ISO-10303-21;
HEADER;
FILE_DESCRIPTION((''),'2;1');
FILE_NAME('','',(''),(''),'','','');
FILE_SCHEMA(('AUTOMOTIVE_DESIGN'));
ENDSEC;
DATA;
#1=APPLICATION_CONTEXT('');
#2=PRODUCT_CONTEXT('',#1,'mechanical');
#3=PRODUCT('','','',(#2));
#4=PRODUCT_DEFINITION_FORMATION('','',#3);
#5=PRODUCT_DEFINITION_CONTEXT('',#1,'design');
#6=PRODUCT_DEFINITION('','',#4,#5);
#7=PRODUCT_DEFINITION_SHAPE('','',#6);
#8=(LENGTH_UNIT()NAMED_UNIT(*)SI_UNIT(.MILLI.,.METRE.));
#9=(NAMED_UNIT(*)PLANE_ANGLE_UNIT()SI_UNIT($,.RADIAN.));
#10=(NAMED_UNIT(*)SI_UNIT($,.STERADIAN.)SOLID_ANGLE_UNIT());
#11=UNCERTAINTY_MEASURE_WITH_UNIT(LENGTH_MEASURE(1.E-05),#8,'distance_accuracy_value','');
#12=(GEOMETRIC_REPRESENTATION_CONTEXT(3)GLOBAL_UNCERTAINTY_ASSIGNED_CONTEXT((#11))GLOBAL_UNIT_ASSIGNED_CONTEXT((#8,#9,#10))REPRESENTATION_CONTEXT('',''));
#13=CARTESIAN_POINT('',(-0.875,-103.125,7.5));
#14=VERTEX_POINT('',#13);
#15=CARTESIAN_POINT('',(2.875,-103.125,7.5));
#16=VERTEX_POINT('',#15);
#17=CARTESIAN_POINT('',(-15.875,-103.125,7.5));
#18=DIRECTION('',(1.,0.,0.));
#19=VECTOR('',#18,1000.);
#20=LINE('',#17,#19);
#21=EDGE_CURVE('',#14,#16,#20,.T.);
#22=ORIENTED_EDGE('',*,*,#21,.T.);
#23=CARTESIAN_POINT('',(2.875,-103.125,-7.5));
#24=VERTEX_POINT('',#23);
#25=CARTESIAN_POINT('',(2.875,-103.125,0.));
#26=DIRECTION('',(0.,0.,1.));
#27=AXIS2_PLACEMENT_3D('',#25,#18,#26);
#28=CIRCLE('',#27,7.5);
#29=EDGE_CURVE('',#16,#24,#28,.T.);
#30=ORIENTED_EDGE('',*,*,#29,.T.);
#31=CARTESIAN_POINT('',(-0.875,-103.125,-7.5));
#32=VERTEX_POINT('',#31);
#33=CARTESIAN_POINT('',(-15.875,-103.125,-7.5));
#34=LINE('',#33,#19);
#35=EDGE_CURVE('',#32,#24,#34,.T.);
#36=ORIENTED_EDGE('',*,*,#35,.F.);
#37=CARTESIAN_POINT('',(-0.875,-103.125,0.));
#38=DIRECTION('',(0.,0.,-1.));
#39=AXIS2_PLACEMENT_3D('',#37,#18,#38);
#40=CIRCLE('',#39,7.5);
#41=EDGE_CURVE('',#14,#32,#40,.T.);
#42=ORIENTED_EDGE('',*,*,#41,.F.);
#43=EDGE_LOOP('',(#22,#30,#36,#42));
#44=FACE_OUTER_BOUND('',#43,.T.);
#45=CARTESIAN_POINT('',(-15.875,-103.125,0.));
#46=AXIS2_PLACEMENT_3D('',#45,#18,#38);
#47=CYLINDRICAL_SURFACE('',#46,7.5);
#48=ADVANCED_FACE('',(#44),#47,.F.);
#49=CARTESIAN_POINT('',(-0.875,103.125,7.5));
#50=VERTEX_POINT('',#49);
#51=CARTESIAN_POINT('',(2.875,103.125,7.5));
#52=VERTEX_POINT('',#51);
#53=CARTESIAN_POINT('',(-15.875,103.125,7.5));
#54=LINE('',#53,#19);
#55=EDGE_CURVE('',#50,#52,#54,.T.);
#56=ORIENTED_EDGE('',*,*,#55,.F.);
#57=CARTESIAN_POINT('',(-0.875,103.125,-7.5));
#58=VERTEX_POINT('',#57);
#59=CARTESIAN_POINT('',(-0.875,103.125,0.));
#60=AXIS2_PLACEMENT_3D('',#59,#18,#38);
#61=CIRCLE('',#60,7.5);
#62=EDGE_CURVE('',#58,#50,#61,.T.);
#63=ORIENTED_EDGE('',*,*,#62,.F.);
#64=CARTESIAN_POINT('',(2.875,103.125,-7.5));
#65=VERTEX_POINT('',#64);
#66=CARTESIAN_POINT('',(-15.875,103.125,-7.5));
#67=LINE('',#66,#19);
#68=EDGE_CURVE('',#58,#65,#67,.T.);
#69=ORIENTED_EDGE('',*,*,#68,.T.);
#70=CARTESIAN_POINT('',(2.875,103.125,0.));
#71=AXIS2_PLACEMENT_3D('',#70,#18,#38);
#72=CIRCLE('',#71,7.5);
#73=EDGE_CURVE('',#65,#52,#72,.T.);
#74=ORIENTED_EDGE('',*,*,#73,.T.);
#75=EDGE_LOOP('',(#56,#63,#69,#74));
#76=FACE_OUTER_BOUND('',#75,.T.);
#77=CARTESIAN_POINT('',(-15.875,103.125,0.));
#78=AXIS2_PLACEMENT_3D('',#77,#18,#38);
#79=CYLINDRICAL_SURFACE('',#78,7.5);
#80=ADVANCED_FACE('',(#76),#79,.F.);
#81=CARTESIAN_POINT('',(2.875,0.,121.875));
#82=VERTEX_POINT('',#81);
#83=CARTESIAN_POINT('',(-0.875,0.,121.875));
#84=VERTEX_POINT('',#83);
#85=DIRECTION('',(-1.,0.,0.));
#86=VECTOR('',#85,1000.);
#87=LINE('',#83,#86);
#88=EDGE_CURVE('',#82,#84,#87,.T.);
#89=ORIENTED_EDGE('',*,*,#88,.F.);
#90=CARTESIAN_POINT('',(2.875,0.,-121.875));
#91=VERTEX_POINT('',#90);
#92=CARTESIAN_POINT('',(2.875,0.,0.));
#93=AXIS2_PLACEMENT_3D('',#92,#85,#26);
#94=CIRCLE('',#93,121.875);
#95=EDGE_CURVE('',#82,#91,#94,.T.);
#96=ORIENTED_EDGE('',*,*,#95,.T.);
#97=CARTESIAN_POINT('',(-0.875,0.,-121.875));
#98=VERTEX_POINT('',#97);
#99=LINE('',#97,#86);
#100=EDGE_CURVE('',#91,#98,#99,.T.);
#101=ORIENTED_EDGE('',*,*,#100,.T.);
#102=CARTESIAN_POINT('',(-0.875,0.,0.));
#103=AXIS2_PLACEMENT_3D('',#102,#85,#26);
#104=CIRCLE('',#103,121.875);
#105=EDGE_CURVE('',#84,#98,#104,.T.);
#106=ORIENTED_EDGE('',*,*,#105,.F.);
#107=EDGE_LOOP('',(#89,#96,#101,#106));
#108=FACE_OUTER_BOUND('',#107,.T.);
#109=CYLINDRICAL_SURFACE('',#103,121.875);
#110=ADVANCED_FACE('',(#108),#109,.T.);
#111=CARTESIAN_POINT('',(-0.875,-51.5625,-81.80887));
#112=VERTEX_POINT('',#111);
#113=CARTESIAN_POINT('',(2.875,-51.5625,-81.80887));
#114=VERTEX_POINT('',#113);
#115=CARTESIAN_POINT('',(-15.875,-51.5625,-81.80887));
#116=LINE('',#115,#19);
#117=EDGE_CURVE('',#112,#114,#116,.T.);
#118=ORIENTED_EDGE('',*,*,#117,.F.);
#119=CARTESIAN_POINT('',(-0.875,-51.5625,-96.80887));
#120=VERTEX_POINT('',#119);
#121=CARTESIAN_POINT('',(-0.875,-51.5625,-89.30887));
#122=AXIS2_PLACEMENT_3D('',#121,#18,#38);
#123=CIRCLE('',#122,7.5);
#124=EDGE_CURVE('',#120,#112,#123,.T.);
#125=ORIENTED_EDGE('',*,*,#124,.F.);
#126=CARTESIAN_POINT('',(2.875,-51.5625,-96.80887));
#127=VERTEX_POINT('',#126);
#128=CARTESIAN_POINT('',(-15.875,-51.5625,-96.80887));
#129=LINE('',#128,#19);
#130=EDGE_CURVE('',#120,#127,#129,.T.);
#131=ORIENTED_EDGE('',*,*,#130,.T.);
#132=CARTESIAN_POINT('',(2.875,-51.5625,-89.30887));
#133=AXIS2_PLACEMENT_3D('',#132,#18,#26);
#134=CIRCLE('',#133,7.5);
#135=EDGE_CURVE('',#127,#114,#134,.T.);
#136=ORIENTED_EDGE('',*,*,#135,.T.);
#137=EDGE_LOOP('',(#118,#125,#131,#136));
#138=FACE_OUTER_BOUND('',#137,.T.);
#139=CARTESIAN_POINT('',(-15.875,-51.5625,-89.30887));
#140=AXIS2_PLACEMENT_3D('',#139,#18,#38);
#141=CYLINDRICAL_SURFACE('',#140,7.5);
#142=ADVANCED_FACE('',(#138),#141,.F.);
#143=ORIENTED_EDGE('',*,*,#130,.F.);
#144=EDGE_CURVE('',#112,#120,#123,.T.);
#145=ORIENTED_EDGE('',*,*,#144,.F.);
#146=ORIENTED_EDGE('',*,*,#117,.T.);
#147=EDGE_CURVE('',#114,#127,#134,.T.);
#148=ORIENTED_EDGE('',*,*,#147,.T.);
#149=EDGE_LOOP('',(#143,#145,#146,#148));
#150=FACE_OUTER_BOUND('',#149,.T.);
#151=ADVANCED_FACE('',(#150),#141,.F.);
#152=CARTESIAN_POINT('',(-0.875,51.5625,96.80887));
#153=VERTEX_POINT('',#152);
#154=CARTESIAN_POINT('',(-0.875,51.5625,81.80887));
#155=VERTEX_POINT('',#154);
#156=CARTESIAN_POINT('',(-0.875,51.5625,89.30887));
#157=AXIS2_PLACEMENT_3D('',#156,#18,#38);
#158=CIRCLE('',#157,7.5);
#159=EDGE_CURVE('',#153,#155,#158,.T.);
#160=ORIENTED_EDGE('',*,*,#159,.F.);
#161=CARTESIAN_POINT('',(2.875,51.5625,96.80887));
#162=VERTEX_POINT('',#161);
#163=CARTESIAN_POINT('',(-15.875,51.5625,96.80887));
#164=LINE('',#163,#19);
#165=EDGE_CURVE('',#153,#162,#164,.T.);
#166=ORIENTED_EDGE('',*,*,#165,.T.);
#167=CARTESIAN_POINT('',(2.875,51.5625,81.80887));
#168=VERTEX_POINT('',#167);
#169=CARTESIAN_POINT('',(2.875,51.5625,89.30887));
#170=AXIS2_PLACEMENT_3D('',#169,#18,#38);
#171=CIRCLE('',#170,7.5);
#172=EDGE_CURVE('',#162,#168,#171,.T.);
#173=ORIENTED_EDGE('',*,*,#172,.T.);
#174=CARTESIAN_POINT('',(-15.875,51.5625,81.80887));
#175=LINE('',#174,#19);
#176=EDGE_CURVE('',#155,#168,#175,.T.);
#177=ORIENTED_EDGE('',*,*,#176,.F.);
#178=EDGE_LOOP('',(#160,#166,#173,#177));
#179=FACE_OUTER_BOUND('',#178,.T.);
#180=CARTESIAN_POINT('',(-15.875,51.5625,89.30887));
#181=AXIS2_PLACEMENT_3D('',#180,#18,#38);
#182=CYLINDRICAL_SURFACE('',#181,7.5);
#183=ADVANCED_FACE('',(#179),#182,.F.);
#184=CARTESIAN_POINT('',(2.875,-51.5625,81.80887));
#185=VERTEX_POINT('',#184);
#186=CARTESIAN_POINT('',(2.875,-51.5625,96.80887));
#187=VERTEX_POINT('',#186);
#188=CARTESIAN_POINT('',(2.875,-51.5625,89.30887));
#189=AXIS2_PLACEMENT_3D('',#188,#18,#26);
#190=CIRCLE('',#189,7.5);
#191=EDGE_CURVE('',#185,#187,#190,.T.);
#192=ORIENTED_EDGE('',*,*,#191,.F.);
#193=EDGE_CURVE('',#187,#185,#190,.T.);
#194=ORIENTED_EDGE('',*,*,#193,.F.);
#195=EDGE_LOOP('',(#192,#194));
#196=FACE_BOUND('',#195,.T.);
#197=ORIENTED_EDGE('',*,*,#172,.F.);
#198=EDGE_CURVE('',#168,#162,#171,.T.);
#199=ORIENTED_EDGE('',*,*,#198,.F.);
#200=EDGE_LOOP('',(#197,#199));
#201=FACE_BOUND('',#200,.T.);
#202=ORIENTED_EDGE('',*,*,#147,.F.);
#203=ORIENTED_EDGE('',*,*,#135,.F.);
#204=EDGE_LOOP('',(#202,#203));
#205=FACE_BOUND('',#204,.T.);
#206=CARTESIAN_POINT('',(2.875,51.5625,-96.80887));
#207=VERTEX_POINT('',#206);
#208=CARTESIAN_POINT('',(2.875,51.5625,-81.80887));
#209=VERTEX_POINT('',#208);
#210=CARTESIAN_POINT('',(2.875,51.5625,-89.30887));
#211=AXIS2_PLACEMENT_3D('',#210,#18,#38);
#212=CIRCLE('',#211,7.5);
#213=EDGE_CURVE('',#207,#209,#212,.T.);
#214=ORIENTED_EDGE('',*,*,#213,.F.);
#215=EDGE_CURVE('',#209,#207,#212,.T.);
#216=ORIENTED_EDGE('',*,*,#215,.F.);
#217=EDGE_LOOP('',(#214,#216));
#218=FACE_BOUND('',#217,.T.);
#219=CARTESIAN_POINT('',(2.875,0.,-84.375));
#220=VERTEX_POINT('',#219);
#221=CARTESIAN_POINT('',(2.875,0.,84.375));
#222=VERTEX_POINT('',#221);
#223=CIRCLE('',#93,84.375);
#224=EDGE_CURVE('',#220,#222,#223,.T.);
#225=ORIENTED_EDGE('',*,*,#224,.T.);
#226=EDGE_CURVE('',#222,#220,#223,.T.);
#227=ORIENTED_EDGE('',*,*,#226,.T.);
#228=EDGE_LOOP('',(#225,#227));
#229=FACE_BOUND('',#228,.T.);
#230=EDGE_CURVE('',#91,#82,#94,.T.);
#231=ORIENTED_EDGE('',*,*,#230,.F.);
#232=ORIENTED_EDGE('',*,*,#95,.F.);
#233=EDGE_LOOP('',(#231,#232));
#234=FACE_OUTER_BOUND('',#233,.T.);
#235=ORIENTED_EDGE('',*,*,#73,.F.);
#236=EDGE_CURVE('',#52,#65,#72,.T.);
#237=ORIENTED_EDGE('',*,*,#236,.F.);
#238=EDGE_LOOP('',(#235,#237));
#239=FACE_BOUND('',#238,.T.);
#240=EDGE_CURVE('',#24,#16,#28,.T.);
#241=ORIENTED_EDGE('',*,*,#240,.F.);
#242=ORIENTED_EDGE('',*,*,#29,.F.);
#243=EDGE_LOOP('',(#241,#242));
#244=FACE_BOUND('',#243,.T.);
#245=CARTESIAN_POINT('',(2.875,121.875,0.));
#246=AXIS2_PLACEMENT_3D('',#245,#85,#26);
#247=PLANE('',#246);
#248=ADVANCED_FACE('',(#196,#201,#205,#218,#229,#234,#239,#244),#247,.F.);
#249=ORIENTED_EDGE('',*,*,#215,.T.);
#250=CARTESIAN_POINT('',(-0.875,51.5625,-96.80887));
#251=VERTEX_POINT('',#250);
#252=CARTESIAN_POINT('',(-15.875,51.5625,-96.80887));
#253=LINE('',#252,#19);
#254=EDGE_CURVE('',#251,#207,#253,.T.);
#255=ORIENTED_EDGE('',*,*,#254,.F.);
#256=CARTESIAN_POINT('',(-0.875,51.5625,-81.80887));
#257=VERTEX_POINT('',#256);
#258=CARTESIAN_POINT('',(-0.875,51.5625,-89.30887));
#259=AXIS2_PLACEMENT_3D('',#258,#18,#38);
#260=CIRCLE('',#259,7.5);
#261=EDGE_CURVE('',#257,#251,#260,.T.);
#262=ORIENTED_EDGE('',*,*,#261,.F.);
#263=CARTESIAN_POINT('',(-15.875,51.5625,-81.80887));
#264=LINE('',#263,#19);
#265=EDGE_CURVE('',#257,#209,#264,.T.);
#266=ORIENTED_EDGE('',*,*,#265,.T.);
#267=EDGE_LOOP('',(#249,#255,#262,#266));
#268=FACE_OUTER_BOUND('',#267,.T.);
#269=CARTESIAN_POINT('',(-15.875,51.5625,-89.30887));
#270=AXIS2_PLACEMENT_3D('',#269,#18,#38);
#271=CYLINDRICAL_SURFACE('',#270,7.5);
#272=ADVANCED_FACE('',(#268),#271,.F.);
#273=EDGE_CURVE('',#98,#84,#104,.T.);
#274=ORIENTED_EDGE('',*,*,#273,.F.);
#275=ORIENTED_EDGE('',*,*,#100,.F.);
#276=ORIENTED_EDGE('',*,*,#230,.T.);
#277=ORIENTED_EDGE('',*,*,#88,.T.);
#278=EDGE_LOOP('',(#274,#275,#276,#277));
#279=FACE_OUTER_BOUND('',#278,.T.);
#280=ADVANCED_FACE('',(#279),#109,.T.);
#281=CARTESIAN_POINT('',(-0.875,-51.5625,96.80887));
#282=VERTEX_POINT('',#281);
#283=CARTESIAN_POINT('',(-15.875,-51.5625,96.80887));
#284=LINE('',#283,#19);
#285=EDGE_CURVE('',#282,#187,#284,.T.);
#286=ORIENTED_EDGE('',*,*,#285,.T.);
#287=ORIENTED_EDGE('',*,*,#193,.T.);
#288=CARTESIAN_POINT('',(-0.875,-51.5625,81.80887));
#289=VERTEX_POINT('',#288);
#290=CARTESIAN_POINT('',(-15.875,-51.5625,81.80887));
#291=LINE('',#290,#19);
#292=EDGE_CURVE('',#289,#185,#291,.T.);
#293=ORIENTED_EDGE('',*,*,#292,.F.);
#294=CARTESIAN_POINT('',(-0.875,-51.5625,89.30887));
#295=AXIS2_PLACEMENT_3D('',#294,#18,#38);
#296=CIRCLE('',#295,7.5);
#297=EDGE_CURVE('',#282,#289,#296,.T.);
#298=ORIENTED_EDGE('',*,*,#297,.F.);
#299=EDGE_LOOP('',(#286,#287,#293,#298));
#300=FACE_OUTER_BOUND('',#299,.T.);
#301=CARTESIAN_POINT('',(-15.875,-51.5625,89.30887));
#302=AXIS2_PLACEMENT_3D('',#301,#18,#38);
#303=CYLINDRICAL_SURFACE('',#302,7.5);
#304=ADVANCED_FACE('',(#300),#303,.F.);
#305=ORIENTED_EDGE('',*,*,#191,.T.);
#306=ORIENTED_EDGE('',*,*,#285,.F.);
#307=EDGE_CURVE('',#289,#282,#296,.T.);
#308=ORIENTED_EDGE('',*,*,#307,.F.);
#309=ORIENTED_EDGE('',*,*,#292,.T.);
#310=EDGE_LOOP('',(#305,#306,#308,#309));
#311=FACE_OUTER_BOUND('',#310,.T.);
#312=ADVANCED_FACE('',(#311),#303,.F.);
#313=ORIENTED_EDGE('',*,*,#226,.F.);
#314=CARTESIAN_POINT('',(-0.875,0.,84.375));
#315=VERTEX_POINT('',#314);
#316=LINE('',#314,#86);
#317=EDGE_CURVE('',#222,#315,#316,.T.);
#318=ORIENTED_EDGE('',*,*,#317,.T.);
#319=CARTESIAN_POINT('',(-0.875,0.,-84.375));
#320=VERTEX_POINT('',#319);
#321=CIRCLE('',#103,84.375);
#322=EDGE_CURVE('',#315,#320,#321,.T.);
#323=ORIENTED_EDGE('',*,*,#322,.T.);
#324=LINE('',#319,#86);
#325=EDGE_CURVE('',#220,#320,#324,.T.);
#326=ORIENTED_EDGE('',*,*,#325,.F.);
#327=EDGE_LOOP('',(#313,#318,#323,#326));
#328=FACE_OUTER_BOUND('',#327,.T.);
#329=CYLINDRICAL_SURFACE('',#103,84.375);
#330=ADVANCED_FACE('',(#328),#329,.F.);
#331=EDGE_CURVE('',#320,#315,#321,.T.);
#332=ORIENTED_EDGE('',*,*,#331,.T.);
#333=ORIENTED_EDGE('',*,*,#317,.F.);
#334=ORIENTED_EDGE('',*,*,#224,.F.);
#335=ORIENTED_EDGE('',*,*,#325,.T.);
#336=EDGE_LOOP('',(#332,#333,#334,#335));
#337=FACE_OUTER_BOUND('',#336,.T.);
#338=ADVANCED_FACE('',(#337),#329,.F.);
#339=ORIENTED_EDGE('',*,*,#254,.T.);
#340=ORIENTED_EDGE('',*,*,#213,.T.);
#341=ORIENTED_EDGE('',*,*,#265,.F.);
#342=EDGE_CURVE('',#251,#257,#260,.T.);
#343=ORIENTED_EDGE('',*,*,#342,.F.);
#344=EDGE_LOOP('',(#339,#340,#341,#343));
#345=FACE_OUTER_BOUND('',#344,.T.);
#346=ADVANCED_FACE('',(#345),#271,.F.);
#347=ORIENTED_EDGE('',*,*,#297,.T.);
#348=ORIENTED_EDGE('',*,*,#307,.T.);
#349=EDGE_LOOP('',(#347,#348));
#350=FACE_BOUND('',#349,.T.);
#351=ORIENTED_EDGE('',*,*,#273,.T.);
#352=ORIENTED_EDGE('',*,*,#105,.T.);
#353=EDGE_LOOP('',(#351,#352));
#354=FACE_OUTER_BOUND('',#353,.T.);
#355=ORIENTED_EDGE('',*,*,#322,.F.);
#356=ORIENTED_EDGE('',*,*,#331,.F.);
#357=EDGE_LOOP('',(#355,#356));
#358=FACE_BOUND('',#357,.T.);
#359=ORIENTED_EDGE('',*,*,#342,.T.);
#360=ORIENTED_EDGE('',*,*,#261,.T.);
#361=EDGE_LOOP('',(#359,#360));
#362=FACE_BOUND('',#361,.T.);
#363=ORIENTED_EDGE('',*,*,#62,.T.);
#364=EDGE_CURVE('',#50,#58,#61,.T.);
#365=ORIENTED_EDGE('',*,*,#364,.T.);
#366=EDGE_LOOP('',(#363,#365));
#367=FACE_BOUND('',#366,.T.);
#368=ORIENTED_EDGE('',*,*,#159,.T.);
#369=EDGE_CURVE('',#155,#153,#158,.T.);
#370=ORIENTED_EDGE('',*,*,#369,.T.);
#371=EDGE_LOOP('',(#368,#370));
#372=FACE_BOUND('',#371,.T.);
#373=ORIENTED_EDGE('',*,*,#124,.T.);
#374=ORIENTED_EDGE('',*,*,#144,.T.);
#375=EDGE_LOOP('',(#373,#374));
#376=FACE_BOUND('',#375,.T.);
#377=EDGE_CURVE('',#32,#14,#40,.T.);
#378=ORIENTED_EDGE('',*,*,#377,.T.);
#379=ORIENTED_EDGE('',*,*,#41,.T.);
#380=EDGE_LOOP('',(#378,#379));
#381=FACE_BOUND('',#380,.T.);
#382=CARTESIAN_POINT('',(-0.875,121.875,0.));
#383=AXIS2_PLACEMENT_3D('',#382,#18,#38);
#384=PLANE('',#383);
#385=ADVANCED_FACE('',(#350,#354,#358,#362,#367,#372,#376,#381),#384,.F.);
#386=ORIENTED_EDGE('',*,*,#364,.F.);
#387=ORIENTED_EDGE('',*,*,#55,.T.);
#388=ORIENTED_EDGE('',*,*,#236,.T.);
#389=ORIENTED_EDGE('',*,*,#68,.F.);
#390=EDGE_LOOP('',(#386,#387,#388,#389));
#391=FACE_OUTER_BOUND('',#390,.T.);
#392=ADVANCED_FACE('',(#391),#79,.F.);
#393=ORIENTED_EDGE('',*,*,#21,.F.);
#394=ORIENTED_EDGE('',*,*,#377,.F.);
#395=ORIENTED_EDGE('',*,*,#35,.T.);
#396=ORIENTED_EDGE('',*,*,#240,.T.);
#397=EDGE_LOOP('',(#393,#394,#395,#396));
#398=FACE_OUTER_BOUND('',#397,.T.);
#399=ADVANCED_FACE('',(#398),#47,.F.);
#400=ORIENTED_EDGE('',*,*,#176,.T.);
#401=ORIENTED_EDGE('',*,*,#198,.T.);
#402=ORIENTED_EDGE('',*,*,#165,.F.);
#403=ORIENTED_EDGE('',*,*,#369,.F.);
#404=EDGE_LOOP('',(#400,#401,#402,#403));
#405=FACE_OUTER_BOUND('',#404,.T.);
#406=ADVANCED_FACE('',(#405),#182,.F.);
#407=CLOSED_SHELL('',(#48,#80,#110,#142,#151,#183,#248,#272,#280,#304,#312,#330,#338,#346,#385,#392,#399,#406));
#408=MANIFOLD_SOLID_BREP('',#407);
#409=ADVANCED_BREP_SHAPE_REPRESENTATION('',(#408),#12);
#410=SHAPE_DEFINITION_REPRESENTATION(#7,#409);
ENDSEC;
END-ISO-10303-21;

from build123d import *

# Parameters (mm, degrees)
SKETCH1_W          = 2
SKETCH1_H          = 20
SKETCH2_R          = 4
CUT_EXTRUDE1_DEPTH = 10
SCALE_1_SCALE      = 1.875


with BuildPart() as part:
    # Sketch1 → Revolve1 (revolve)
    with BuildSketch(Plane.XY, mode=Mode.PRIVATE) as revolve1_sk:
        with Locations((1, 55)):
            Rectangle(SKETCH1_W, SKETCH1_H)
    revolve(revolve1_sk.sketch.rotate(Axis((0, 0, 0), (1, 0, 0)), 90), axis=Axis((0, 0, 0), (1, 0, 0)))

    # Sketch2 → Cut-Extrude1 (cut)
    with BuildSketch(Plane(origin=(2, 0, 0), x_dir=(0, 0, -1), z_dir=(1, 0, 0))):
        with Locations((0, 55)):
            Circle(SKETCH2_R)
        with Locations((47.631397208, 27.5)):
            Circle(SKETCH2_R)
        with Locations((-47.631397208, 27.5)):
            Circle(SKETCH2_R)
        with Locations((47.631397208, -27.5)):
            Circle(SKETCH2_R)
        with Locations((-47.631397208, -27.5)):
            Circle(SKETCH2_R)
        with Locations((0, -55)):
            Circle(SKETCH2_R)
    extrude(amount=-CUT_EXTRUDE1_DEPTH, mode=Mode.SUBTRACT)


with BuildPart() as part_1:
    # Scale 1: scaled about (1, 0, 0)
    add(part.part.scale(SCALE_1_SCALE).moved(Location((-0.875, 0, 0))))


solid = part_1.part
